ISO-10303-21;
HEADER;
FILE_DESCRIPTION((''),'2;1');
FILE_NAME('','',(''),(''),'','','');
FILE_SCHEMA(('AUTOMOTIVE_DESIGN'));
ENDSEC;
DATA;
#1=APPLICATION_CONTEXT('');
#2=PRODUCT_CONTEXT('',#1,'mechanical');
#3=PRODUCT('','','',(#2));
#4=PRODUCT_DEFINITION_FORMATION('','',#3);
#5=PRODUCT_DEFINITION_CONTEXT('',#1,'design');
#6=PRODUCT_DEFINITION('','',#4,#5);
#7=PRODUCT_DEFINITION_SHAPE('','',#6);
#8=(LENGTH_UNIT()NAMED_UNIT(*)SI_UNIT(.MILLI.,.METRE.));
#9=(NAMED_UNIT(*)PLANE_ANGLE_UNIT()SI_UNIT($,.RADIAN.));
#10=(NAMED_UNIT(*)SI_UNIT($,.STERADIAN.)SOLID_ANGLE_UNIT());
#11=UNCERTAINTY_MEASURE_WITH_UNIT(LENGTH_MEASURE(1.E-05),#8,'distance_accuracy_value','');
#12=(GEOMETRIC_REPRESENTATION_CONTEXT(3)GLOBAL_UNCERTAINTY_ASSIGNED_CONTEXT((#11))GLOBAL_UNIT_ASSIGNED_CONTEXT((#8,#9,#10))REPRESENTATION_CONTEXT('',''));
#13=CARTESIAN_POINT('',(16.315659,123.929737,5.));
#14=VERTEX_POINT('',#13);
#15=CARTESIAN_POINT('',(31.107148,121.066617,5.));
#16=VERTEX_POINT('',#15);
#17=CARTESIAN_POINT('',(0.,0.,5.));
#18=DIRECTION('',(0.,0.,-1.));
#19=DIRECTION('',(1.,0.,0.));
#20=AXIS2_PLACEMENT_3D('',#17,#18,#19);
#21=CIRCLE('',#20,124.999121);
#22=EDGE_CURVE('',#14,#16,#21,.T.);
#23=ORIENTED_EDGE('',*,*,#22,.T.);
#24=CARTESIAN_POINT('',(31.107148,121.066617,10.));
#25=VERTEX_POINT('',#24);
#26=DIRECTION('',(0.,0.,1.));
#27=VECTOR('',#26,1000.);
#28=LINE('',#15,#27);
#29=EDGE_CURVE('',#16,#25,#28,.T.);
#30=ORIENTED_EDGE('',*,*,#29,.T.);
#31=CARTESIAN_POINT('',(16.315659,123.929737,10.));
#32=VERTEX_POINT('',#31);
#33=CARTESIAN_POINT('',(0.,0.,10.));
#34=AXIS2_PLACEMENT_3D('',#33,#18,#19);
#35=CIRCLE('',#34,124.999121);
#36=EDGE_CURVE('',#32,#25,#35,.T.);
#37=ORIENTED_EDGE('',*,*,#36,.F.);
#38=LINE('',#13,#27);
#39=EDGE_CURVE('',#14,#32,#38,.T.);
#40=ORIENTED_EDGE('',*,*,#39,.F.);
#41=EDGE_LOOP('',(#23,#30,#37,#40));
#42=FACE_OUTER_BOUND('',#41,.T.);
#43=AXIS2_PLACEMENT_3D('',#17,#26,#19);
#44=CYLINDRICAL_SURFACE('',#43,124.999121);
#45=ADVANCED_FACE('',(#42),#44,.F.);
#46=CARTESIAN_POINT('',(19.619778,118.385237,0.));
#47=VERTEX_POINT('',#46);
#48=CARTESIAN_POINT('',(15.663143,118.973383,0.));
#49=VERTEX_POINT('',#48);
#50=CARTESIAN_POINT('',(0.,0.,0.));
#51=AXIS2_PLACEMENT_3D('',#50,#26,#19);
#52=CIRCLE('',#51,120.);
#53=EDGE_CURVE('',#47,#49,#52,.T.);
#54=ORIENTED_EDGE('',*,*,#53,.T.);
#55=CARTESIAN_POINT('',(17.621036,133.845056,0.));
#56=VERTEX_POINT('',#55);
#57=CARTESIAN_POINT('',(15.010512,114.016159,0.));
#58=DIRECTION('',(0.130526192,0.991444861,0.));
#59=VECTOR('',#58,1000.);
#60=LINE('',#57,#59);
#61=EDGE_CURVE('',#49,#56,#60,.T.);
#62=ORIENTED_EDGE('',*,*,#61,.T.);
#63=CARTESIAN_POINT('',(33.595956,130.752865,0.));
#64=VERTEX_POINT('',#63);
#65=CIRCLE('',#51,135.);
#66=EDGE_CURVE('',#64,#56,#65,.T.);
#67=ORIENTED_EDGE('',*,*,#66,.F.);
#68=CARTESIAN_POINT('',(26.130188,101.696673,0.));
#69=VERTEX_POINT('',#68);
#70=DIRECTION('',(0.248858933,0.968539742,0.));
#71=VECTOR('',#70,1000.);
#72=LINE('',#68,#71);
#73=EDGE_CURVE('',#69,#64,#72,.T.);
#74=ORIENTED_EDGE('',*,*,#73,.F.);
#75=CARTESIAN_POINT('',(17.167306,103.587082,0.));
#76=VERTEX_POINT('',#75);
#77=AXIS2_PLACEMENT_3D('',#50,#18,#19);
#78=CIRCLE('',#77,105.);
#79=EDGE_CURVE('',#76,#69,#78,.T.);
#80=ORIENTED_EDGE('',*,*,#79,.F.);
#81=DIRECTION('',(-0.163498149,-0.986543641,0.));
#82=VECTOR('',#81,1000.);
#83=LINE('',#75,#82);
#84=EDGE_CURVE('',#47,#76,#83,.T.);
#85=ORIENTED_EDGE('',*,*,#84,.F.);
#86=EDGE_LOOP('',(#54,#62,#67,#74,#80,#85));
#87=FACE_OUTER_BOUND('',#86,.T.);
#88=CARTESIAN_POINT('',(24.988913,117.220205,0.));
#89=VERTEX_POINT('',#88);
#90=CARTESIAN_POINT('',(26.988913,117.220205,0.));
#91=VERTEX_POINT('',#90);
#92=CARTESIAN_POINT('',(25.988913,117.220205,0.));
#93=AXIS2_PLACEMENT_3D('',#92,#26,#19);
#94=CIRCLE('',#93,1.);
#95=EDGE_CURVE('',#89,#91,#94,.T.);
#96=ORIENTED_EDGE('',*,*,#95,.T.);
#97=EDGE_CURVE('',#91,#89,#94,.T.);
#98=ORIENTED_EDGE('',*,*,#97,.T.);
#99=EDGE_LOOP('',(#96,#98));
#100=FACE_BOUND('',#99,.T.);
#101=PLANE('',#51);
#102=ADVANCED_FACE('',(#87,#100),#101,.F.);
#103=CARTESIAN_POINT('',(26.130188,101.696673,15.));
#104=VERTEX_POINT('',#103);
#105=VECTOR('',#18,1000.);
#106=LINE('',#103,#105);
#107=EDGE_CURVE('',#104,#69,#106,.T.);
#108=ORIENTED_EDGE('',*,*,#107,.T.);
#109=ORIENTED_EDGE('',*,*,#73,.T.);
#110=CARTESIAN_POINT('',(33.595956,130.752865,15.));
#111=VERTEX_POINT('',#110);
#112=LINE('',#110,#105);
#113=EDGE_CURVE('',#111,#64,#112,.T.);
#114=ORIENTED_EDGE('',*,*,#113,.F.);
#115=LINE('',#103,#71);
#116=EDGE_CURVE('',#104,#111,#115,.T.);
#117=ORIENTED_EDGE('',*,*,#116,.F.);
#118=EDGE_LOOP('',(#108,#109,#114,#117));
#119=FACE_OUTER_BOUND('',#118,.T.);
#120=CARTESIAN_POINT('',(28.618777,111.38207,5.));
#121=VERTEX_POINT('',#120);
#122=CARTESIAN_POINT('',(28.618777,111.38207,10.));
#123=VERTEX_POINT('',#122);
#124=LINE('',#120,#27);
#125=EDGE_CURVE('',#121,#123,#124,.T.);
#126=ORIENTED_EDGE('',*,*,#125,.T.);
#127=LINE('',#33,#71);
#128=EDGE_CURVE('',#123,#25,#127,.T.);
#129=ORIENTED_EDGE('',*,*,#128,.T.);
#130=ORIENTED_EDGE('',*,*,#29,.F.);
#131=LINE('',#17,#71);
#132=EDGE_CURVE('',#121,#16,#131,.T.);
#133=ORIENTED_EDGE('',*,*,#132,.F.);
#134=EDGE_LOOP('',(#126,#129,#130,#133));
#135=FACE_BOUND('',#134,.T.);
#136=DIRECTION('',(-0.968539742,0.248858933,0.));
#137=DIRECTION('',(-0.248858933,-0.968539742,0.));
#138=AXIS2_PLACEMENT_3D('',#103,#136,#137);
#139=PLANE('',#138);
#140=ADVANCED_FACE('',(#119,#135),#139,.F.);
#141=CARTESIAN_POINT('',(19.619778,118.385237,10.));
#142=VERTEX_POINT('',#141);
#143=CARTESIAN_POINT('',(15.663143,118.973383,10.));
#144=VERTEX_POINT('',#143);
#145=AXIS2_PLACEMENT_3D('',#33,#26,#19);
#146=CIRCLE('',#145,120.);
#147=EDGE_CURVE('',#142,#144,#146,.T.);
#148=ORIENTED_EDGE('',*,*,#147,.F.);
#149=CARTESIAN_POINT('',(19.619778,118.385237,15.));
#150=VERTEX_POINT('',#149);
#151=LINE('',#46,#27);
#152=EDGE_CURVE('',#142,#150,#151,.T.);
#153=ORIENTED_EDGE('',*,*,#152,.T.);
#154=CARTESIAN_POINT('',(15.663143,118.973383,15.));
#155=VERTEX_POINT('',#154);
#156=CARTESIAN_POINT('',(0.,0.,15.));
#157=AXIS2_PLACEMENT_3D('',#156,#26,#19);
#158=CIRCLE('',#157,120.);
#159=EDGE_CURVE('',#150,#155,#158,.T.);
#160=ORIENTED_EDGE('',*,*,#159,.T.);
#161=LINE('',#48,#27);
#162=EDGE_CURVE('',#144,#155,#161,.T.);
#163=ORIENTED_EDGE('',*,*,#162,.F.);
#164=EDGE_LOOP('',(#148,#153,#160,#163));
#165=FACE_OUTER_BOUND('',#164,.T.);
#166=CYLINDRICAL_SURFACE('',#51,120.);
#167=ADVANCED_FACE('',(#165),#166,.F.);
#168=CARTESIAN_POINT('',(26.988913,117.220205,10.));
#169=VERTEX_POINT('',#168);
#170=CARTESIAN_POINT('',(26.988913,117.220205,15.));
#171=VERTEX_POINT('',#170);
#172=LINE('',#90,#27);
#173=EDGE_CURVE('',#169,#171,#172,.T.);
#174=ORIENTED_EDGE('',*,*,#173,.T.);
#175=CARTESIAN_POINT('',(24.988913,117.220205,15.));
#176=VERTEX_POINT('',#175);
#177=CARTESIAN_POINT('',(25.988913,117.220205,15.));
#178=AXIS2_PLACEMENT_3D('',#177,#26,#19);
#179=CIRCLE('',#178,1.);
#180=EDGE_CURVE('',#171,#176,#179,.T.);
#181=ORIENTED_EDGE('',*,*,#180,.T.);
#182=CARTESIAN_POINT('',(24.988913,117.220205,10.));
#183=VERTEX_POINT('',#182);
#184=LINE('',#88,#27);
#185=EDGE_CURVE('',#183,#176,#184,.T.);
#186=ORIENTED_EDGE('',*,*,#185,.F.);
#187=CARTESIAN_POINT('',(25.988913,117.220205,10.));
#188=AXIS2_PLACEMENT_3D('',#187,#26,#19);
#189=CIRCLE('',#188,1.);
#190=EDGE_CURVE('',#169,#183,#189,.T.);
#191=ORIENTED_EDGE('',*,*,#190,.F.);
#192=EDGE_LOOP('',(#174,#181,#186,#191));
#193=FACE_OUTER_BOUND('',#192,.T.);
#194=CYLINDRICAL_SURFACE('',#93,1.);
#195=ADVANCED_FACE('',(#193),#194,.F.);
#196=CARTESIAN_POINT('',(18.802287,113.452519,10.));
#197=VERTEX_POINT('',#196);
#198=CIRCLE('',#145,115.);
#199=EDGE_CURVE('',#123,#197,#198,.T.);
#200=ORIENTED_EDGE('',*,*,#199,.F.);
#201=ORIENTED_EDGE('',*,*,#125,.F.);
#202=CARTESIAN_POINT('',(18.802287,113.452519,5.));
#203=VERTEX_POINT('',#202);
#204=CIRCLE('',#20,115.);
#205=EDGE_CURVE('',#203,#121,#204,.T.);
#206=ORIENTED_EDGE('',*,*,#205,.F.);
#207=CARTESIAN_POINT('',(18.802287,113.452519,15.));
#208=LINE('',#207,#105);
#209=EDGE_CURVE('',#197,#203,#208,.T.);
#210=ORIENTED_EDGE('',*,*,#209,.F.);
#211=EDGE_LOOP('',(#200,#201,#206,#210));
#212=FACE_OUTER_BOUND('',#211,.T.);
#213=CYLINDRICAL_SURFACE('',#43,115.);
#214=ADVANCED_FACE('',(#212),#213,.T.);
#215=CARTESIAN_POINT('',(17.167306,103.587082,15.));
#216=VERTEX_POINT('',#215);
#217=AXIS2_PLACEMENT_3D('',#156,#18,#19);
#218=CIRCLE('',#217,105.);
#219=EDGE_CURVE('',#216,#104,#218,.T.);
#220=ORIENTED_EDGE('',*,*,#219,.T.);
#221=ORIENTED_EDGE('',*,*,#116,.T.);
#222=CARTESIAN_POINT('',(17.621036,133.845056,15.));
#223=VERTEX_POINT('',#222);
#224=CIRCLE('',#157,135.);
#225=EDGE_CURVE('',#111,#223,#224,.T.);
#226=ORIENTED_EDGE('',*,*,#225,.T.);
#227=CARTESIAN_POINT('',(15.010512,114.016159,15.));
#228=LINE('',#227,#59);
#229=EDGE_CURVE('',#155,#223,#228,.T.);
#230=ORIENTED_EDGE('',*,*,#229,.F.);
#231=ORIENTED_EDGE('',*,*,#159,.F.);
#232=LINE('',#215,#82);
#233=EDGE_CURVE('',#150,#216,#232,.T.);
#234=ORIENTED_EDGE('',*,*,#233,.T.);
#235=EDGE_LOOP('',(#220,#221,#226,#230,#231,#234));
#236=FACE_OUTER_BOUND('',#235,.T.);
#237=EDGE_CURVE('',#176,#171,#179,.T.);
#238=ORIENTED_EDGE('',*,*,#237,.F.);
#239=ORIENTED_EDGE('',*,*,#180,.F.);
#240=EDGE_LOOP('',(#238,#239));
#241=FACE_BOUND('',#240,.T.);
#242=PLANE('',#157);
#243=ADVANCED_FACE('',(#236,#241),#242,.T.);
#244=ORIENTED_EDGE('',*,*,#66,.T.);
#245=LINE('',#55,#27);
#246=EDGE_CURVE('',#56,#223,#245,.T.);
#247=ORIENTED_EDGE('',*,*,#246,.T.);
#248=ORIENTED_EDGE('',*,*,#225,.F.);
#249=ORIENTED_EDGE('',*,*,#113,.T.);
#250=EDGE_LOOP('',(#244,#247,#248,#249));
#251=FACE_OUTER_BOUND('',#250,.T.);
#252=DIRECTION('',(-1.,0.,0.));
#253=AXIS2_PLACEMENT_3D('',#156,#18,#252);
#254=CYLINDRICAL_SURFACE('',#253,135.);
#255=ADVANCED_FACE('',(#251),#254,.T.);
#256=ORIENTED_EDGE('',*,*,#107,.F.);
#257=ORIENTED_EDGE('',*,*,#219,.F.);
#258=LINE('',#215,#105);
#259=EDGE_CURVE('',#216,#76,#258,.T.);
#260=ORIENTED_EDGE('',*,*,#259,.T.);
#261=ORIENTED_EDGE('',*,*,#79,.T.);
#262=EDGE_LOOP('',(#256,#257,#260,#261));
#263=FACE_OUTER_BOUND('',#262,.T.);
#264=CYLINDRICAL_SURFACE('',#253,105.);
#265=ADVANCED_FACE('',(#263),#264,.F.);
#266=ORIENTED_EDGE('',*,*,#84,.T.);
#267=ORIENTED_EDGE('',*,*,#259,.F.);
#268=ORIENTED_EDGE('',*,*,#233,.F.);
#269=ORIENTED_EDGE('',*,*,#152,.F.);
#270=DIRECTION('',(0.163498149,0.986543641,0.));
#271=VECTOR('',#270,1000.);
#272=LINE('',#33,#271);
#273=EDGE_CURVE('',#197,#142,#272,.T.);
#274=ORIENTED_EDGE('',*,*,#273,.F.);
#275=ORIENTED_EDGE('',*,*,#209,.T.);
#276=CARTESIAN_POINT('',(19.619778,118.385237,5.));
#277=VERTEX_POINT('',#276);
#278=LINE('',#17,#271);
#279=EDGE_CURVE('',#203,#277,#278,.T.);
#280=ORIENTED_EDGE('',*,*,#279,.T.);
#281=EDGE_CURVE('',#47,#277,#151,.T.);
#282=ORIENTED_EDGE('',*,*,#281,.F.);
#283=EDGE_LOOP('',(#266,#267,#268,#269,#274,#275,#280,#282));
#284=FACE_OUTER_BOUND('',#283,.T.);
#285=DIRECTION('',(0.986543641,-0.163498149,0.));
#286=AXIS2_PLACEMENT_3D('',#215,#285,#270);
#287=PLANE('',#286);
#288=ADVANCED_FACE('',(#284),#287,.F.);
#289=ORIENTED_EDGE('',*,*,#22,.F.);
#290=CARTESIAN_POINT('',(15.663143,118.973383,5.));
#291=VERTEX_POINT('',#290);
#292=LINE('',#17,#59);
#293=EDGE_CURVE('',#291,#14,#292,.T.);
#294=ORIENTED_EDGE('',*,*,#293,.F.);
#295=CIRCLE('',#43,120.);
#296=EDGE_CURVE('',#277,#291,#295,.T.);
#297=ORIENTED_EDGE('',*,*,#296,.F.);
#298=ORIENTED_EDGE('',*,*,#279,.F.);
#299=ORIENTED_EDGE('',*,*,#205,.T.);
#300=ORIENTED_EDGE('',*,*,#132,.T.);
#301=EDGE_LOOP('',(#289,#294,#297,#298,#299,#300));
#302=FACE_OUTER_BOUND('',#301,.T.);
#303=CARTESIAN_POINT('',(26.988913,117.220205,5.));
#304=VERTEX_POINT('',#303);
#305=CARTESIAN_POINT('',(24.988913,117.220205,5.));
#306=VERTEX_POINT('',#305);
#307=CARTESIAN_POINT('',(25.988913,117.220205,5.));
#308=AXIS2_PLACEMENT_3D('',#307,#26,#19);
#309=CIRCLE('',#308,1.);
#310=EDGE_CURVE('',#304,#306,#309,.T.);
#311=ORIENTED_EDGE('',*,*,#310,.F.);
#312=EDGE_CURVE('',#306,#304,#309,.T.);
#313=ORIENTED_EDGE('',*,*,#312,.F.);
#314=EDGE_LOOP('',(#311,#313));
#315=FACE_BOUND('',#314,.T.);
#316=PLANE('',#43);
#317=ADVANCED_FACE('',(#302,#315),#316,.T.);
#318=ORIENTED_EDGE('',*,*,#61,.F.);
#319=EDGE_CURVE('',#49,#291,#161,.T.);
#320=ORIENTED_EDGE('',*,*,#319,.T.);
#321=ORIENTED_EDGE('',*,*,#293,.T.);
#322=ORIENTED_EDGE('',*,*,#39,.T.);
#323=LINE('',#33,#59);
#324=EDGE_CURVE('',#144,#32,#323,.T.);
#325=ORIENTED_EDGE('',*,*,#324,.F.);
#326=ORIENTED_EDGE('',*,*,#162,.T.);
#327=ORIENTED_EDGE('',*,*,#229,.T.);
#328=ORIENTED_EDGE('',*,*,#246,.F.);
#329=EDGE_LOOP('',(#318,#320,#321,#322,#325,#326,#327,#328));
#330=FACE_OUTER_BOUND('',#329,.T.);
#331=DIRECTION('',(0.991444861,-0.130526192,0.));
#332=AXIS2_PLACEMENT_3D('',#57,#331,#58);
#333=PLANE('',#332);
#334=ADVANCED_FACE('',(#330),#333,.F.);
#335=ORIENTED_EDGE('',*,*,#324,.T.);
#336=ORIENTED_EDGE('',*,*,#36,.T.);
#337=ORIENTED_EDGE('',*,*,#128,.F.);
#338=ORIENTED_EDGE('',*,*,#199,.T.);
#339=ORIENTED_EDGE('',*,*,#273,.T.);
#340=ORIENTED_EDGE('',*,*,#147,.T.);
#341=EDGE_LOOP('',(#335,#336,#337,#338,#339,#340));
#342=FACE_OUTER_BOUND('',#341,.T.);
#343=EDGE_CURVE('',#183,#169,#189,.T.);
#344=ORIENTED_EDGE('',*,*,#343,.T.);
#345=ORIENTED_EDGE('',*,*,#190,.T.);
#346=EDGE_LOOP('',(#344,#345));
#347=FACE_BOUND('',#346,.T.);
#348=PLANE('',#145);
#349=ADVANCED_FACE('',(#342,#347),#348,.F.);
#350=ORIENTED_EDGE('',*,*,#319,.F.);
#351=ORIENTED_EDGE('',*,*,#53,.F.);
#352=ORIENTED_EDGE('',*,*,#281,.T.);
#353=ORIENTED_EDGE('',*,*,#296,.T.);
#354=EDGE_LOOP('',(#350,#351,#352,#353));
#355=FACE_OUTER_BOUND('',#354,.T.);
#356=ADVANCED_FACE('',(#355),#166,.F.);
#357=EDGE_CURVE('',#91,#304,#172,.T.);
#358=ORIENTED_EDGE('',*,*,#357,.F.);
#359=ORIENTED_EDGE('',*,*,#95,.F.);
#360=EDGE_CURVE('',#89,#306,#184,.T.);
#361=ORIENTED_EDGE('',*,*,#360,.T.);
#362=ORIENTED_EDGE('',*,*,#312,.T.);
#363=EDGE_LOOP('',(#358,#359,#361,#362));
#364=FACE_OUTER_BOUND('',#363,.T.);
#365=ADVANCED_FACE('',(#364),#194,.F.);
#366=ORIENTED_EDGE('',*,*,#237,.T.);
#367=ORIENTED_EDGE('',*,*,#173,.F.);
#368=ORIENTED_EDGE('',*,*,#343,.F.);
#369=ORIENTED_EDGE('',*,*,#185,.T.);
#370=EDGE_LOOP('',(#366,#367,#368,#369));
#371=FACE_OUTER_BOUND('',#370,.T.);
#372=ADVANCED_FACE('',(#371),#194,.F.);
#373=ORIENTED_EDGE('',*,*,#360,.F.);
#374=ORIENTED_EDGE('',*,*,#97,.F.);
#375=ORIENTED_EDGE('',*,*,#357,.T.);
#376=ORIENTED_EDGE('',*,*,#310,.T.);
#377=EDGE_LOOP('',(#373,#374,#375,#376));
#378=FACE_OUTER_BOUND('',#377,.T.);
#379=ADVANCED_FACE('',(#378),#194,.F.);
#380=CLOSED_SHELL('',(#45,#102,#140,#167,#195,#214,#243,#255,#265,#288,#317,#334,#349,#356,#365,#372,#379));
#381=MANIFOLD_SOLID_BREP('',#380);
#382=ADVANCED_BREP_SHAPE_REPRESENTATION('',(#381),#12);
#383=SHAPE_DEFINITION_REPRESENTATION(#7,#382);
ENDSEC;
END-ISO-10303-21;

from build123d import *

# Parameters (mm, degrees)
BOSS_EXTRUDE1_DEPTH = 15
CUT_EXTRUDE1_START  = -10
CUT_EXTRUDE1_DEPTH  = 10
BOSS_EXTRUDE3_START = -5
BOSS_EXTRUDE3_DEPTH = 5
SKETCH5_R           = 1
CUT_EXTRUDE2_DEPTH  = 15
CUT_EXTRUDE4_START  = -15
CUT_EXTRUDE4_DEPTH  = 15
CUT_EXTRUDE5_START  = -15
CUT_EXTRUDE5_DEPTH  = 15


with BuildPart() as part:
    # Sketch1 → Boss-Extrude1 (new body)
    with BuildSketch(Plane.XY):
        with BuildLine():
            Line((6.964115375, 114.788941528), (9.188776982, 134.686919846))
            ThreePointArc((9.188776982, 134.686919846), (21.482610172, 133.279771384), (33.595955959, 130.752865143))
            Line((33.595955959, 130.752865143), (26.130187968, 101.696672889))
            ThreePointArc((26.130187968, 101.696672889), (21.669371251, 102.739662982), (17.167305653, 103.587082286))
            Line((17.167305653, 103.587082286), (18.802287144, 113.452518695))
            ThreePointArc((18.802287144, 113.452518695), (12.90051864, 114.274129263), (6.964115375, 114.788941528))
        make_face()
    extrude(amount=BOSS_EXTRUDE1_DEPTH)

    # Sketch3 → Cut-Extrude1 (cut)
    with BuildSketch(Plane.XY.offset(15).offset(CUT_EXTRUDE1_START)):
        with BuildLine():
            ThreePointArc((18.802287144, 113.452518695), (23.733120893, 112.52439279), (28.618777298, 111.382070307))
            Line((28.618777298, 111.382070307), (31.107147965, 121.066616705))
            ThreePointArc((31.107147965, 121.066616705), (19.677605268, 123.440561348), (8.076446178, 124.737930687))
            Line((8.076446178, 124.737930687), (6.964115375, 114.788941528))
            ThreePointArc((6.964115375, 114.788941528), (12.90051864, 114.274129263), (18.802287144, 113.452518695))
        make_face()
    extrude(amount=CUT_EXTRUDE1_DEPTH, mode=Mode.SUBTRACT)

    # Sketch4 → Boss-Extrude3 (add)
    with BuildSketch(Plane.XY.offset(15).offset(BOSS_EXTRUDE3_START)):
        with BuildLine():
            ThreePointArc((28.618777298, 111.382070307), (17.872807715, 113.602652893), (6.964115375, 114.788941528))
            Line((6.964115375, 114.788941528), (8.076446178, 124.737930687))
            ThreePointArc((8.076446178, 124.737930687), (19.677605268, 123.440561348), (31.107147965, 121.066616705))
            Line((31.107147965, 121.066616705), (28.618777298, 111.382070307))
        make_face()
    extrude(amount=BOSS_EXTRUDE3_DEPTH)

    # Sketch5 → Cut-Extrude2 (cut)
    with BuildSketch(Plane.XY.offset(15)):
        with Locations((25.988912996, 117.220204748)):
            Circle(SKETCH5_R)
    extrude(amount=-CUT_EXTRUDE2_DEPTH, mode=Mode.SUBTRACT)

    # Sketch7 → Cut-Extrude4 (cut)
    with BuildSketch(Plane.XY.offset(15).offset(CUT_EXTRUDE4_START)):
        with BuildLine():
            Line((0, 115), (0, 135))
            ThreePointArc((0, 135), (8.829422446, 134.710954637), (17.62103595, 133.845056285))
            Line((17.62103595, 133.845056285), (15.010512105, 114.016159058))
            ThreePointArc((15.010512105, 114.016159058), (7.521359861, 114.753776172), (0, 115))
        make_face()
    extrude(amount=CUT_EXTRUDE4_DEPTH, mode=Mode.SUBTRACT)

    # Sketch8 → Cut-Extrude5 (cut)
    with BuildSketch(Plane.XY.offset(15).offset(CUT_EXTRUDE5_START)):
        with BuildLine():
            Line((15.010512105, 114.016159058), (15.663143066, 118.973383365))
            ThreePointArc((15.663143066, 118.973383365), (17.643911325, 118.695797706), (19.619777889, 118.385236899))
            Line((19.619777889, 118.385236899), (18.802287144, 113.452518695))
            ThreePointArc((18.802287144, 113.452518695), (16.908748354, 113.750139469), (15.010512105, 114.016159058))
        make_face()
    extrude(amount=CUT_EXTRUDE5_DEPTH, mode=Mode.SUBTRACT)


solid = part.part
